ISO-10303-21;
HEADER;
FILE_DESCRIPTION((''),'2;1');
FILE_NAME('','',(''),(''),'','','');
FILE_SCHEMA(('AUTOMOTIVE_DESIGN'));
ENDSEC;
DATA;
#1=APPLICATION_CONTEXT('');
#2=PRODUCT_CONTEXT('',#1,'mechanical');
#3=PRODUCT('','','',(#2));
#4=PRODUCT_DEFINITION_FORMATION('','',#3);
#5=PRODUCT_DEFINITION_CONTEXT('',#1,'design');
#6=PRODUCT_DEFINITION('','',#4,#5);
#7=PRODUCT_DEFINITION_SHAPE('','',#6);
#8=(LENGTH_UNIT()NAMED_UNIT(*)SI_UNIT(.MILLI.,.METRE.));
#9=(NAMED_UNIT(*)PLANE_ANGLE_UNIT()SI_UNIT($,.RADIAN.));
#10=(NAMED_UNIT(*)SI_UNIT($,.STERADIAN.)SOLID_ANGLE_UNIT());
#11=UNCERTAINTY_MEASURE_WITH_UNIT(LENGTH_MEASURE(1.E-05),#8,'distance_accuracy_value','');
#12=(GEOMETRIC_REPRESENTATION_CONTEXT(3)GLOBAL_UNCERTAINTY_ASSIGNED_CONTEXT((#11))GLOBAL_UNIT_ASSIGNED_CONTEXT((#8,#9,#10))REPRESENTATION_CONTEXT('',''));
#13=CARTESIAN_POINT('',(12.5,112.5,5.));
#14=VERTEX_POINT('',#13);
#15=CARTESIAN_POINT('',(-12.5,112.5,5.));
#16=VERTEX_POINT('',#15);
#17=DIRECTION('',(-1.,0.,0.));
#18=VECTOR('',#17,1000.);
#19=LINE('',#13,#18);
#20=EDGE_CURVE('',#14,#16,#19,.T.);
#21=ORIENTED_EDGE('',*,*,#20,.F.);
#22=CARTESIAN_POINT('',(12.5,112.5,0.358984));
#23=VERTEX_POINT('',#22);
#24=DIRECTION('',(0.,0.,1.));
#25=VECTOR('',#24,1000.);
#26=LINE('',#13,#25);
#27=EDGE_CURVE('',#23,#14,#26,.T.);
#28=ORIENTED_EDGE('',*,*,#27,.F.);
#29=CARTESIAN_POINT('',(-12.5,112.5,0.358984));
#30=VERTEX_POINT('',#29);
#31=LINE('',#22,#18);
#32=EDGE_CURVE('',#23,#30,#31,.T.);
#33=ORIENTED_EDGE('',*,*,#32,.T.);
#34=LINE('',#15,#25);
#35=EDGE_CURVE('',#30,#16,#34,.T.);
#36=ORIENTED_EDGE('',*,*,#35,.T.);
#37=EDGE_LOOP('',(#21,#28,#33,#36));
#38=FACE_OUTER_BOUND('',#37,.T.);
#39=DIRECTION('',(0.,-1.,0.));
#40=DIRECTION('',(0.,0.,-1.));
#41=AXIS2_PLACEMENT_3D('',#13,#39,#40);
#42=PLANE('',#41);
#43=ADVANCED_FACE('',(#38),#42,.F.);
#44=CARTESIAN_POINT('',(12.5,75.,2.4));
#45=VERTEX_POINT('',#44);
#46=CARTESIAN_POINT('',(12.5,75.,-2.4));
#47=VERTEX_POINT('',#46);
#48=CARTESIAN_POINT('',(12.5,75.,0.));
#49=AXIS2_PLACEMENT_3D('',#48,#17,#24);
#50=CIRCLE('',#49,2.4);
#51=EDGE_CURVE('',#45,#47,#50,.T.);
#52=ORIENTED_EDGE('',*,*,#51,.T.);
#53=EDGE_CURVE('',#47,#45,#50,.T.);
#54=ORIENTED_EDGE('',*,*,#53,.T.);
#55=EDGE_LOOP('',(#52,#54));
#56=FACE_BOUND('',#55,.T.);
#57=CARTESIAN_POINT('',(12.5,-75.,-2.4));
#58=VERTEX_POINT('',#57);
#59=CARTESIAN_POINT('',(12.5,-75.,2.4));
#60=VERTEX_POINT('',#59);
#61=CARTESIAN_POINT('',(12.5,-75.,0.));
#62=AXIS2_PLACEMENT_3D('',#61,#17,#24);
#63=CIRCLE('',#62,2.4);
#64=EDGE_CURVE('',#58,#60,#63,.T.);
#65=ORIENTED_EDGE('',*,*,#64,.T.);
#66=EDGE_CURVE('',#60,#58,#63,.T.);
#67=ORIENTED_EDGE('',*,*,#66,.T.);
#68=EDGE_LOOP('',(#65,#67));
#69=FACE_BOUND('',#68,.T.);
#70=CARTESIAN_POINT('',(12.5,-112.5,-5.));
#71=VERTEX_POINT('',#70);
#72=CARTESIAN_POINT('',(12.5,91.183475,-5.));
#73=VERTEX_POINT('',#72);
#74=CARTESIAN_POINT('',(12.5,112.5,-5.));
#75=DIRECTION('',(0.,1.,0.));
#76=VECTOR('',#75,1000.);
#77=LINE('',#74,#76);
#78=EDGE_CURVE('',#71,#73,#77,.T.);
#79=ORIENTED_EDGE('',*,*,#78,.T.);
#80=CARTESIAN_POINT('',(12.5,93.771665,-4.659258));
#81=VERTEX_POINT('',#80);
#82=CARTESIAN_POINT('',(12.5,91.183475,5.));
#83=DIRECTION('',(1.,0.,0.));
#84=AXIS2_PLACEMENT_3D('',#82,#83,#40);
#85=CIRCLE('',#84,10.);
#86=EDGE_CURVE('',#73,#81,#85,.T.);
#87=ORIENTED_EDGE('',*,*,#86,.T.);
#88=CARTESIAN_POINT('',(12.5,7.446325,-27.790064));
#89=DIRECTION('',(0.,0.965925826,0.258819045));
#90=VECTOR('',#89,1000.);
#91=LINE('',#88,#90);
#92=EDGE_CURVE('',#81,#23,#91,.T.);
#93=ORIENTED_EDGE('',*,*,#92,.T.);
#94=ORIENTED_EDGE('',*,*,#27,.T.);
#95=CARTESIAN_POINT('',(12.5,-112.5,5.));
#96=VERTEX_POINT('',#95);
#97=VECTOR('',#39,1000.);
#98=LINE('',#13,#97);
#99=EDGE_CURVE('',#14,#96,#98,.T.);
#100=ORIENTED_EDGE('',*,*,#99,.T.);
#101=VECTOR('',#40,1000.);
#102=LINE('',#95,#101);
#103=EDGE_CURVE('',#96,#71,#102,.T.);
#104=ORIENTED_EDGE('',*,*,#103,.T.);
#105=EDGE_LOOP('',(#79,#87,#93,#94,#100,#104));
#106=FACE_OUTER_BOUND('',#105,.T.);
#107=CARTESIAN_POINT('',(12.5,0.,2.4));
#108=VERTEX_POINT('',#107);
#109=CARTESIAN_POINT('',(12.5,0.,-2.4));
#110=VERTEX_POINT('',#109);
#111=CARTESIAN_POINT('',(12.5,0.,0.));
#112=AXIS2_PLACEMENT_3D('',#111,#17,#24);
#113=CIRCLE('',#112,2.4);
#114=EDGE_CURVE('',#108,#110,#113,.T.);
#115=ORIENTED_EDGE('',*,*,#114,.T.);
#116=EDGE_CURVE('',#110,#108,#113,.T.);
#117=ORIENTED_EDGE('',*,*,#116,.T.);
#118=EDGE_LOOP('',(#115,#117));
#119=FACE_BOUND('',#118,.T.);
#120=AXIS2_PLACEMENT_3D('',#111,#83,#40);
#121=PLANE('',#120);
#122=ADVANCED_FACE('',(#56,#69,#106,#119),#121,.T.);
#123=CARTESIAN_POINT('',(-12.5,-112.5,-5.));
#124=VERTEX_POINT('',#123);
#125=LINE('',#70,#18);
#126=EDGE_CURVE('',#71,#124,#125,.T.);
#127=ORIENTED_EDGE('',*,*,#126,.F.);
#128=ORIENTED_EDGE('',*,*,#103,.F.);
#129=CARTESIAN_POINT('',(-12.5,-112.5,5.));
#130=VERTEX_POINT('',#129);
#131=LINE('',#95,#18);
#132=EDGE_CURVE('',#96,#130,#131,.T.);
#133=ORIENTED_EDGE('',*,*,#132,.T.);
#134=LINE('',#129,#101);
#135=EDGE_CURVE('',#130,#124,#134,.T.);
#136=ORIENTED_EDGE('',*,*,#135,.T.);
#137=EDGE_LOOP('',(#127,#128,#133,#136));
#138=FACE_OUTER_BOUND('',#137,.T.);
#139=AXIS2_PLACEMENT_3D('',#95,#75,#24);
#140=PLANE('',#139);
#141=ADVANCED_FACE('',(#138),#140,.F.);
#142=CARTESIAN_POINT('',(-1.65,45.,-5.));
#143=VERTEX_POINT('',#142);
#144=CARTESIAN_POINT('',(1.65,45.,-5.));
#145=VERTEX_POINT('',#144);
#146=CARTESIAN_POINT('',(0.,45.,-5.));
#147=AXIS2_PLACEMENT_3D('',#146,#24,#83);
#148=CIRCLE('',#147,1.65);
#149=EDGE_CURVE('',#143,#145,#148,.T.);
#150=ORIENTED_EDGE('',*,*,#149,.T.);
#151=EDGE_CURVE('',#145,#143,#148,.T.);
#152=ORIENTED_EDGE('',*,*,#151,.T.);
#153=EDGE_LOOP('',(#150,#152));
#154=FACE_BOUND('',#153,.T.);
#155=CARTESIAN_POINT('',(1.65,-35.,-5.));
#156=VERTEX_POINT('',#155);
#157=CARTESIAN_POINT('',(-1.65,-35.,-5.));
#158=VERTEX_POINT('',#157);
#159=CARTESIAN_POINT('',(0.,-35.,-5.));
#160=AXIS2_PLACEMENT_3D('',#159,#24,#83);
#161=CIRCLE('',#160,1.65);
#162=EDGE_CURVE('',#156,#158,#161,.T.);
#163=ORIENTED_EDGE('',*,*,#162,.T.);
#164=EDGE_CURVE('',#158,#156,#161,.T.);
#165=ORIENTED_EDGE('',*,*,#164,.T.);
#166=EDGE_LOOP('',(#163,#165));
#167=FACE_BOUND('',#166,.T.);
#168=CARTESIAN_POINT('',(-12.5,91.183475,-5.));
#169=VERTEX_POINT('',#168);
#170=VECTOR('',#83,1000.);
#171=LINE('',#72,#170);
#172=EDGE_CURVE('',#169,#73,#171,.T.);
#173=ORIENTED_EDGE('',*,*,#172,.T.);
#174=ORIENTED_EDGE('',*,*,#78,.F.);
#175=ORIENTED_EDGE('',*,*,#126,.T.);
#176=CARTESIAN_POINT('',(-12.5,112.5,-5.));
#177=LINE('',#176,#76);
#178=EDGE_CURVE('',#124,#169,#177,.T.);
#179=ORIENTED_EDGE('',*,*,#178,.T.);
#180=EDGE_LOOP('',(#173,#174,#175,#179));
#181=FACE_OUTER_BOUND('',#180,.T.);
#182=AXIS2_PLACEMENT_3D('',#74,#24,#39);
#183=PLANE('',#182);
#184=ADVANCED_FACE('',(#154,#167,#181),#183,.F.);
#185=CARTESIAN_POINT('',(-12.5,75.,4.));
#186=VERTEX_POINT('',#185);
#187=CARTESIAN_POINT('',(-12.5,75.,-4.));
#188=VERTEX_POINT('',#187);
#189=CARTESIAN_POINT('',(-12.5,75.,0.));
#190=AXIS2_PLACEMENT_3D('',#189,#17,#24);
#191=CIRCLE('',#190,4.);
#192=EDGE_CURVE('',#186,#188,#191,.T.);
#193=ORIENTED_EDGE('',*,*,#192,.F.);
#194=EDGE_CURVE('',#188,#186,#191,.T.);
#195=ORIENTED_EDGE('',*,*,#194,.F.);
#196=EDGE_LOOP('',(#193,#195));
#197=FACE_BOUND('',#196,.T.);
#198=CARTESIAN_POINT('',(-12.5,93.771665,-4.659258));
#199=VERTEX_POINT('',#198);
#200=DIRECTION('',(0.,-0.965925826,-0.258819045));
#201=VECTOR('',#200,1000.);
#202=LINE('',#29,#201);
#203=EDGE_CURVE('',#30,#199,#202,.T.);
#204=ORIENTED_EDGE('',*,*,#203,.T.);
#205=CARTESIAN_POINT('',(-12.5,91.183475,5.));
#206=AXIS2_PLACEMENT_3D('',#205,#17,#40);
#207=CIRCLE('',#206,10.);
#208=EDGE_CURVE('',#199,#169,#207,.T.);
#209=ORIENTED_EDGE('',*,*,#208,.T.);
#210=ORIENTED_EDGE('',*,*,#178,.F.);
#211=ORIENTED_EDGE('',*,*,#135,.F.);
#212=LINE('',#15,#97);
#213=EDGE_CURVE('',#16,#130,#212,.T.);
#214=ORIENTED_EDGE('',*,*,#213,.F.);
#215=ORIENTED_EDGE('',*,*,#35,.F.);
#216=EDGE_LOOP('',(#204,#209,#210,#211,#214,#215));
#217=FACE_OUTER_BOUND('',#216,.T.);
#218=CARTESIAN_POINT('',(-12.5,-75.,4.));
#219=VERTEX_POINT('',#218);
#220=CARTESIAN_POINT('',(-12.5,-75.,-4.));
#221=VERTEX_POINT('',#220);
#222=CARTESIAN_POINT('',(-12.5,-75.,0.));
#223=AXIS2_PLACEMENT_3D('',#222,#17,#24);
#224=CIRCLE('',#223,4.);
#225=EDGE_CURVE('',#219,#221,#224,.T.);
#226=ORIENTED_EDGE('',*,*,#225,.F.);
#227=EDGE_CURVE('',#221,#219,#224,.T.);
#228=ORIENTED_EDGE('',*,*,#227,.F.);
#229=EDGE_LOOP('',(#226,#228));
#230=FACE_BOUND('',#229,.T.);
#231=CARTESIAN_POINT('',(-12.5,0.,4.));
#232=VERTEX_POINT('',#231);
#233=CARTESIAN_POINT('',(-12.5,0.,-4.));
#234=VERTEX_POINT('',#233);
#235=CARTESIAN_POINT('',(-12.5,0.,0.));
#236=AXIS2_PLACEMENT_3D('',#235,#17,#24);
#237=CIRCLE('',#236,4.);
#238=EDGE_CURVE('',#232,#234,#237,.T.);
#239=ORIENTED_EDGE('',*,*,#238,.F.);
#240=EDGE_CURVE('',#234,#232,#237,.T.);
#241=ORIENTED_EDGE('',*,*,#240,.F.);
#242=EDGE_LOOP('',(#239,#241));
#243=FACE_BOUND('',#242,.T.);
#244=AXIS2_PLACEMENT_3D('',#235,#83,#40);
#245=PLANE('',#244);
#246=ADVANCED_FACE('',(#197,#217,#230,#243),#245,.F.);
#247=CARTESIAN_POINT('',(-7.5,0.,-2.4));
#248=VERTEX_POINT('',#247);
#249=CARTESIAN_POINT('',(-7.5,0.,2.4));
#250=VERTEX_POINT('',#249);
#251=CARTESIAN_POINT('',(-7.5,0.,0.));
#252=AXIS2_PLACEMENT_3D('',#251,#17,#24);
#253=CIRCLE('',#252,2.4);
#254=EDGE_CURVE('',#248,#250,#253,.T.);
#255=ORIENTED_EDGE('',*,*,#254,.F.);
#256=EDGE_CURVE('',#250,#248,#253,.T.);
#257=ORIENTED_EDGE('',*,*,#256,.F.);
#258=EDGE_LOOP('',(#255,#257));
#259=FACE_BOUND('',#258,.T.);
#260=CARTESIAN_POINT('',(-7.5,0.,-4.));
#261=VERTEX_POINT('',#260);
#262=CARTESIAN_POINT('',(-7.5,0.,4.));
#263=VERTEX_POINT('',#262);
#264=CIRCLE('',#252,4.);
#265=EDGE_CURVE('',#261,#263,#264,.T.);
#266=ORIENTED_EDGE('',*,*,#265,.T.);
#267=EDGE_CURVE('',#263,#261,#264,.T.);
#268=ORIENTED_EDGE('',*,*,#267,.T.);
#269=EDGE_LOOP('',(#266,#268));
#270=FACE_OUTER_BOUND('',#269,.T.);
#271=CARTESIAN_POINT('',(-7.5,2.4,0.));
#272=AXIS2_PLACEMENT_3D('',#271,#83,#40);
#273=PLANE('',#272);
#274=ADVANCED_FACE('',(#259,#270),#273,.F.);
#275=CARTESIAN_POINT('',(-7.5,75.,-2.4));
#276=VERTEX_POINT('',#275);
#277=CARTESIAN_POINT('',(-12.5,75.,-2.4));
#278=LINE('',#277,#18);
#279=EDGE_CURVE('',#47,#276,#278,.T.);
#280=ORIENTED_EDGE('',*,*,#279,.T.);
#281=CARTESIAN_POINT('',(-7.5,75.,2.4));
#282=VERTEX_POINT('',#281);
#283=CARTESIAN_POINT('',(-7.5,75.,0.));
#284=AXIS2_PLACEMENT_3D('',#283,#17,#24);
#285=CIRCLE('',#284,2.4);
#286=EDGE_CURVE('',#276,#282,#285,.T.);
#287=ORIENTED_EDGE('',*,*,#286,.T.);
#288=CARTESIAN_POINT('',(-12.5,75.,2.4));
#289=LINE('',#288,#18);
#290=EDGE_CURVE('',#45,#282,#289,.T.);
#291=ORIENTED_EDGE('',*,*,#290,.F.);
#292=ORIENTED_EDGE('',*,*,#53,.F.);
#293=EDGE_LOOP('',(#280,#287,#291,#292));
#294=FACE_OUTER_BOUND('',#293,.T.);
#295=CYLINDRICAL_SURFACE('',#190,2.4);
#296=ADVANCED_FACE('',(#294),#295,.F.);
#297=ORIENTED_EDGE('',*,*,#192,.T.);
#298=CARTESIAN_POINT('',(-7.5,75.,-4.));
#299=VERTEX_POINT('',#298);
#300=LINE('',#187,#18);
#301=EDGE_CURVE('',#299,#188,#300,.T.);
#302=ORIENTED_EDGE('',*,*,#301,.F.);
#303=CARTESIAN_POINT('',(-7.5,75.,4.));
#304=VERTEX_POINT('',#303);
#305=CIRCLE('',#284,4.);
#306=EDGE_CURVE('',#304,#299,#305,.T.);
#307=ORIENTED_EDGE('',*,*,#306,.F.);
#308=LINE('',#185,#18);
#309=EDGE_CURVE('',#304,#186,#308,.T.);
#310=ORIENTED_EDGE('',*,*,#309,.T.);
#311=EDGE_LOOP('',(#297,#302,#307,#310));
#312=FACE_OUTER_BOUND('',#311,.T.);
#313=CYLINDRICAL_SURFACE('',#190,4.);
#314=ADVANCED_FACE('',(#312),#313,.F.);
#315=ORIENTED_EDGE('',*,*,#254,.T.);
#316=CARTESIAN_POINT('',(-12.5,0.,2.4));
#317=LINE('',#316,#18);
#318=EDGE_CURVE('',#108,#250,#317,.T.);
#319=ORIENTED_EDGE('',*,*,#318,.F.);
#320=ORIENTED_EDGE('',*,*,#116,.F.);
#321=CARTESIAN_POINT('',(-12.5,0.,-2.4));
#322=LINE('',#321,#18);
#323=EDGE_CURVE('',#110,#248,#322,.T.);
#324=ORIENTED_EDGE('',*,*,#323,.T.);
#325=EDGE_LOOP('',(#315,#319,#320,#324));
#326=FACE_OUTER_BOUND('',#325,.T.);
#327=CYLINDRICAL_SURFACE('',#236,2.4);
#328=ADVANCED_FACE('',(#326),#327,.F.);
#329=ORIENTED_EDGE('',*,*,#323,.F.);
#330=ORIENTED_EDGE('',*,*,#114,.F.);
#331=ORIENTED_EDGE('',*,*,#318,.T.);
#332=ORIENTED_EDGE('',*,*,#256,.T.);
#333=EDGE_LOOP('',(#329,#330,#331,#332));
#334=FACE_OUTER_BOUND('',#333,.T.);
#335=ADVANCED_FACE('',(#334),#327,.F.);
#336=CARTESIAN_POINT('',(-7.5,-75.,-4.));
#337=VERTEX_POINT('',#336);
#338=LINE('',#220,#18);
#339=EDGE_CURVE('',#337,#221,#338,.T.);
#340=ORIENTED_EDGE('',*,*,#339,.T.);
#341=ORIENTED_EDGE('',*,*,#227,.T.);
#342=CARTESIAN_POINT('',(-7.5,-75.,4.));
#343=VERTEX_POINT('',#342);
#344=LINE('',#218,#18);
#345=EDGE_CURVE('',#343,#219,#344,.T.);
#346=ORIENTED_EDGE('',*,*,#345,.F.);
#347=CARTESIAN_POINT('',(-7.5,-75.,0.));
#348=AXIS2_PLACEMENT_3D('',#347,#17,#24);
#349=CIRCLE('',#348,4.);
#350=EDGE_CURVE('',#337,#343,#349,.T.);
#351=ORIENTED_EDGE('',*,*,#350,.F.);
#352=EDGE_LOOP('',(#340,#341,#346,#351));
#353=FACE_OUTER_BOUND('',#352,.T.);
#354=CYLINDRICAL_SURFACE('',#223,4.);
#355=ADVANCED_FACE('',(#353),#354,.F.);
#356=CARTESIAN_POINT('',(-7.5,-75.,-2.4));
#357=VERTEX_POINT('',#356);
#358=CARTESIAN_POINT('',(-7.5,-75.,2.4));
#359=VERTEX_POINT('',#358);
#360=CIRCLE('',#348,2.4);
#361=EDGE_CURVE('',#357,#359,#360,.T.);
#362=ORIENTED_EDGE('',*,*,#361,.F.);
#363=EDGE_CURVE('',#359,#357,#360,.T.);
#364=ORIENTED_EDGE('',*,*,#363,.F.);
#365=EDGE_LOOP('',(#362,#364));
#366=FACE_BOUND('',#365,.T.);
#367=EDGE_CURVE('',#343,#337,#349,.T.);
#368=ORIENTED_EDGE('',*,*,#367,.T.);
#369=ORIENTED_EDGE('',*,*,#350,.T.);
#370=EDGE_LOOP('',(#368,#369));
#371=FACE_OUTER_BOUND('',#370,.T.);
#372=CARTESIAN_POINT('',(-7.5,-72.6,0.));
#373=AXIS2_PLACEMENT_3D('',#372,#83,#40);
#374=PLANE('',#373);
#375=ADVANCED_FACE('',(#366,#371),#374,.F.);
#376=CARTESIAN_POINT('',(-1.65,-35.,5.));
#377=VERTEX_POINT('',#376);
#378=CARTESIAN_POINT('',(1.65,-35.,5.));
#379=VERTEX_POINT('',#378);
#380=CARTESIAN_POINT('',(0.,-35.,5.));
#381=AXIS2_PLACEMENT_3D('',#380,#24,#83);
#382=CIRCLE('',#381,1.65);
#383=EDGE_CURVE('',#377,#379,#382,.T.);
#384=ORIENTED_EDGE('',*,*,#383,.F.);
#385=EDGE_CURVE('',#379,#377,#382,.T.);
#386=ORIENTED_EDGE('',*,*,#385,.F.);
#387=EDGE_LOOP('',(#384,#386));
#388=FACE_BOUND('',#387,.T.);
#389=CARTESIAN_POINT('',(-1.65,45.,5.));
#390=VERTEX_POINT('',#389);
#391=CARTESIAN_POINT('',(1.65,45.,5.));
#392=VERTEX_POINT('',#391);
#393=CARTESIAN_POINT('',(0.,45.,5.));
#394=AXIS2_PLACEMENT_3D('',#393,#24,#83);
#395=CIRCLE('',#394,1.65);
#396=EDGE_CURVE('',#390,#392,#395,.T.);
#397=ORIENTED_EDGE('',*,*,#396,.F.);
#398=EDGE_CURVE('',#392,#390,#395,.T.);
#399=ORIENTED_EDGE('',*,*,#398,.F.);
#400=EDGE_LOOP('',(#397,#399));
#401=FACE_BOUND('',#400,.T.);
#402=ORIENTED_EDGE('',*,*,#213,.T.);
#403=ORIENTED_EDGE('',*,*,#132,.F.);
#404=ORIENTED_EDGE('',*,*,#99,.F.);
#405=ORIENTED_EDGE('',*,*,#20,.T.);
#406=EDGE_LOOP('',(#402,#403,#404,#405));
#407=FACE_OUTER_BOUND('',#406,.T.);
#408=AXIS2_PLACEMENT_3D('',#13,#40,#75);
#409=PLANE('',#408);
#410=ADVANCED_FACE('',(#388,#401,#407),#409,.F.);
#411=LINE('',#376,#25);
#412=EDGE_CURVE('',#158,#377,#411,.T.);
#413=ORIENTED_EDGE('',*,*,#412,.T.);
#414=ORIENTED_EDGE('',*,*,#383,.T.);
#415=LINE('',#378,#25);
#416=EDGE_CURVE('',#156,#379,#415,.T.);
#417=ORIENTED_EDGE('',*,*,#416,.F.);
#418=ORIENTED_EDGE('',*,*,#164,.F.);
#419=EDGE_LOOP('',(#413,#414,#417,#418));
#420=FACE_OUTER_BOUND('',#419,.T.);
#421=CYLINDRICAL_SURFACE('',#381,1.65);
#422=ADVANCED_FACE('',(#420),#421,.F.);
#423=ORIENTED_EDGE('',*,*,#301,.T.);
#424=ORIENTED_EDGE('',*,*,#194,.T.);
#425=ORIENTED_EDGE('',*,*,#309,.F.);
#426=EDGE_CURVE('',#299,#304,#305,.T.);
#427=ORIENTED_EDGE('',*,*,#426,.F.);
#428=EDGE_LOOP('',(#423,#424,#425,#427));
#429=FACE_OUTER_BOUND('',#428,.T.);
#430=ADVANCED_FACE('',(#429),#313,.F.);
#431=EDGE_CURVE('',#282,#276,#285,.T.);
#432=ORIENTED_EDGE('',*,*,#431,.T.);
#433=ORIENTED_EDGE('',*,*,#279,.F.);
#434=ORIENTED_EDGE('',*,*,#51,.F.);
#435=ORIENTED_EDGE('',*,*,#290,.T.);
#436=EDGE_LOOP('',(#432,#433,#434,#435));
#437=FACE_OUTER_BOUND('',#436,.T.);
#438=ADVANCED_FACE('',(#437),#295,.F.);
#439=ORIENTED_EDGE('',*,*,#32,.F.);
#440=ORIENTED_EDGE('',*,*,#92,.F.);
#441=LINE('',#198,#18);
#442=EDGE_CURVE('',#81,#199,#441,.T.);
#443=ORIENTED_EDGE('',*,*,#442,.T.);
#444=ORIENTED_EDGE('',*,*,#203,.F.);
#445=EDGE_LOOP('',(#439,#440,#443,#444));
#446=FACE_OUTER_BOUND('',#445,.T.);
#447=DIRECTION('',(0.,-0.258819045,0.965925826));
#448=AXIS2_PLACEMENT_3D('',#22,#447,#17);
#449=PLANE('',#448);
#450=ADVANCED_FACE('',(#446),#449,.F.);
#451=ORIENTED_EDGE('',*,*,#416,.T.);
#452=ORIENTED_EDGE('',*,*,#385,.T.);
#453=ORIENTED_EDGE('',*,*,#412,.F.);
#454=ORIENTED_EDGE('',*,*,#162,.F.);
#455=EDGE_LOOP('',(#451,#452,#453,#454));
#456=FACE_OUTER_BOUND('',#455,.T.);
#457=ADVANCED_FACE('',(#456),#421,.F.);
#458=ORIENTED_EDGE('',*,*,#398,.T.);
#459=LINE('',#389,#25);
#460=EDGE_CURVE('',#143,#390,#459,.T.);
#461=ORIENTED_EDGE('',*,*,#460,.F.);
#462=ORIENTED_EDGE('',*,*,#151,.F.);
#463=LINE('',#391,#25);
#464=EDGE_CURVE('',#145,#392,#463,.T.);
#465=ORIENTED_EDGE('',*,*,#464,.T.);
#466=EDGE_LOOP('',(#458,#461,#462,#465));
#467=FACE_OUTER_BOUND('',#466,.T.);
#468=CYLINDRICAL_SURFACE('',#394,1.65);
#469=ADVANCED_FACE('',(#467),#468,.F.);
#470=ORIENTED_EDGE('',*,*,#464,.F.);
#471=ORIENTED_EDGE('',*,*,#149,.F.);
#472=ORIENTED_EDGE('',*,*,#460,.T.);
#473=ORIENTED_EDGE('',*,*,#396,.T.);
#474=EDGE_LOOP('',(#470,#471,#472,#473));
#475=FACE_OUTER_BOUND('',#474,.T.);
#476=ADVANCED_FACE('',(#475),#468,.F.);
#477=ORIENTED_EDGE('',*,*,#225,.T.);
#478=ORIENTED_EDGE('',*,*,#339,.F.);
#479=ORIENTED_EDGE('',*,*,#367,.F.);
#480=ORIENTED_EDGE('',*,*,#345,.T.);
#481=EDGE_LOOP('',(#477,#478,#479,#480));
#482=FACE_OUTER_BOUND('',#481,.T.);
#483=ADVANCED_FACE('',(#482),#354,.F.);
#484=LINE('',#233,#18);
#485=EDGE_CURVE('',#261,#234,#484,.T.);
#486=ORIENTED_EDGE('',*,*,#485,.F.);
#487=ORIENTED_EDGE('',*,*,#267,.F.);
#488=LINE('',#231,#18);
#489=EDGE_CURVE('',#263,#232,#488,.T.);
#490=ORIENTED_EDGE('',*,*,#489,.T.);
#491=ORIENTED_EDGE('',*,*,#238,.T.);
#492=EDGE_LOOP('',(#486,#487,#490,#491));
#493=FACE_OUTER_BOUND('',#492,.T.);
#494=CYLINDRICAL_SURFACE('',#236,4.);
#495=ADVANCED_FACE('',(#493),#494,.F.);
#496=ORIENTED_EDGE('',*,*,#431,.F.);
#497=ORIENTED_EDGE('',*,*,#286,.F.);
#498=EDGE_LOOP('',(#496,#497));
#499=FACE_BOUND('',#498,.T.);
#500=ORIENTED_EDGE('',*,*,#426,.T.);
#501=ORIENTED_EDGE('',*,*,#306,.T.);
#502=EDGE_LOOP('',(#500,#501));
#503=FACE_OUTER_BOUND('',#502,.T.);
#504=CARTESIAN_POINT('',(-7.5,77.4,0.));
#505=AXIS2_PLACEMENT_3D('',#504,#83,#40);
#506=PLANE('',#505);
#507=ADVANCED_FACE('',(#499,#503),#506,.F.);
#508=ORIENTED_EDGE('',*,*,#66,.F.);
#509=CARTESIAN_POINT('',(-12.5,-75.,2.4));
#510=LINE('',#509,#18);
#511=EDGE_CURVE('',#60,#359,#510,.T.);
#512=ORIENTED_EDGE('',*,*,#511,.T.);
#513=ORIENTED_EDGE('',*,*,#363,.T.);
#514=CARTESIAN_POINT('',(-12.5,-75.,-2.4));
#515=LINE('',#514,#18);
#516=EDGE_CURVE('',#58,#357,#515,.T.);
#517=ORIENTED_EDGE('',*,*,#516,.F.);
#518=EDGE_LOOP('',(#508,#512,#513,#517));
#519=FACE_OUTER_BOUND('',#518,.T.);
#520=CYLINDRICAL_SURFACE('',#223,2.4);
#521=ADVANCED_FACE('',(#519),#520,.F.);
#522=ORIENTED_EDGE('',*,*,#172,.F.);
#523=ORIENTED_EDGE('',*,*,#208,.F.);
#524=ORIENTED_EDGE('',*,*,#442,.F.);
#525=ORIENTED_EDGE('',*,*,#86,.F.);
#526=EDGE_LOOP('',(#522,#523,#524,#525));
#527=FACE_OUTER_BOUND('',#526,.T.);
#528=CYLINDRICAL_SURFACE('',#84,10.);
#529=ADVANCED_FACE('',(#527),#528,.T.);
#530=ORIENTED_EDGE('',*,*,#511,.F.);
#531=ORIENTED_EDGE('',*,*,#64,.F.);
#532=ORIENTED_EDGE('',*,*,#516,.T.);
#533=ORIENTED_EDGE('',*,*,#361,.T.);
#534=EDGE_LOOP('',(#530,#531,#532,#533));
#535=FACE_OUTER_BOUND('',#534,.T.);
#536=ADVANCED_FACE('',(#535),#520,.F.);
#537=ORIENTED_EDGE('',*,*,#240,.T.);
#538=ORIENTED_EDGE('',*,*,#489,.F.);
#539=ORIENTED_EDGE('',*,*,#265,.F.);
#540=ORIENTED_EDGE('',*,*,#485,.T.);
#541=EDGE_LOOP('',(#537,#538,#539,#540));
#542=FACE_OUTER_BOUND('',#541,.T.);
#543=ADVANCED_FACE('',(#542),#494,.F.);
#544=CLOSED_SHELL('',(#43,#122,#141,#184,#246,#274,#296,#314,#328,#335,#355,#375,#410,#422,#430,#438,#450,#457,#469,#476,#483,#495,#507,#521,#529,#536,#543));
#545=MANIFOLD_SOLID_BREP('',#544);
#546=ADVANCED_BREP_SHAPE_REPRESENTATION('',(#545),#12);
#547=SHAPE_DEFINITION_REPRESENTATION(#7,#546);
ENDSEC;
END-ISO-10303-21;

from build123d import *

# Parameters (mm, degrees)
SKETCH_1_W                = 10
SKETCH_1_H                = 225
EXTRUDE_1_DEPTH           = 12.5
CHAMFER_1_SIZE            = 20
CHAMFER_1_SIZE2           = 5.358983849
HOLE_WIZARD_1_D           = 4.8
HOLE_WIZARD_1_CBORE_D     = 8
HOLE_WIZARD_1_CBORE_DEPTH = 5
HOLE_WIZARD_M4_1_D        = 3.3
FILLET_1_R                = 10


with BuildPart() as part:
    # 草图1 → 凸台-拉伸1 (new, symmetric)
    with BuildSketch(Plane(origin=(0, 0, 0), x_dir=(0, 0, -1), z_dir=(1, 0, 0))):
        Rectangle(SKETCH_1_W, SKETCH_1_H)
    extrude(amount=EXTRUDE_1_DEPTH, both=True)

    # 倒角1
    chamfer_1_edges = [part.edges().sort_by_distance(p)[0] for p in [
        (0, 112.5, -5),
    ]]
    chamfer_1_side = [part.faces().sort_by_distance(p)[0] for p in [
        (0, 0, -5),
    ]]
    chamfer(chamfer_1_edges, length=CHAMFER_1_SIZE, length2=CHAMFER_1_SIZE2, reference=chamfer_1_side[0])

    # 打孔尺寸(%根据)开槽圆柱头螺钉的类型1 (through all)
    with Locations(Plane.ZY.offset(12.5)):
        with Locations((0, 75), (0, 0), (0, -75)):
            CounterBoreHole(HOLE_WIZARD_1_D / 2, HOLE_WIZARD_1_CBORE_D / 2, HOLE_WIZARD_1_CBORE_DEPTH)

    # M4 螺纹孔1 (through all)
    with Locations(Plane.XY.offset(5)):
        with Locations((0, 45), (0, -35)):
            Hole(HOLE_WIZARD_M4_1_D / 2)

    # 圆角1
    fillet_1_edges = [part.edges().sort_by_distance(p)[0] for p in [
        (0, 92.5, -5),
    ]]
    fillet(fillet_1_edges, radius=FILLET_1_R)


solid = part.part
